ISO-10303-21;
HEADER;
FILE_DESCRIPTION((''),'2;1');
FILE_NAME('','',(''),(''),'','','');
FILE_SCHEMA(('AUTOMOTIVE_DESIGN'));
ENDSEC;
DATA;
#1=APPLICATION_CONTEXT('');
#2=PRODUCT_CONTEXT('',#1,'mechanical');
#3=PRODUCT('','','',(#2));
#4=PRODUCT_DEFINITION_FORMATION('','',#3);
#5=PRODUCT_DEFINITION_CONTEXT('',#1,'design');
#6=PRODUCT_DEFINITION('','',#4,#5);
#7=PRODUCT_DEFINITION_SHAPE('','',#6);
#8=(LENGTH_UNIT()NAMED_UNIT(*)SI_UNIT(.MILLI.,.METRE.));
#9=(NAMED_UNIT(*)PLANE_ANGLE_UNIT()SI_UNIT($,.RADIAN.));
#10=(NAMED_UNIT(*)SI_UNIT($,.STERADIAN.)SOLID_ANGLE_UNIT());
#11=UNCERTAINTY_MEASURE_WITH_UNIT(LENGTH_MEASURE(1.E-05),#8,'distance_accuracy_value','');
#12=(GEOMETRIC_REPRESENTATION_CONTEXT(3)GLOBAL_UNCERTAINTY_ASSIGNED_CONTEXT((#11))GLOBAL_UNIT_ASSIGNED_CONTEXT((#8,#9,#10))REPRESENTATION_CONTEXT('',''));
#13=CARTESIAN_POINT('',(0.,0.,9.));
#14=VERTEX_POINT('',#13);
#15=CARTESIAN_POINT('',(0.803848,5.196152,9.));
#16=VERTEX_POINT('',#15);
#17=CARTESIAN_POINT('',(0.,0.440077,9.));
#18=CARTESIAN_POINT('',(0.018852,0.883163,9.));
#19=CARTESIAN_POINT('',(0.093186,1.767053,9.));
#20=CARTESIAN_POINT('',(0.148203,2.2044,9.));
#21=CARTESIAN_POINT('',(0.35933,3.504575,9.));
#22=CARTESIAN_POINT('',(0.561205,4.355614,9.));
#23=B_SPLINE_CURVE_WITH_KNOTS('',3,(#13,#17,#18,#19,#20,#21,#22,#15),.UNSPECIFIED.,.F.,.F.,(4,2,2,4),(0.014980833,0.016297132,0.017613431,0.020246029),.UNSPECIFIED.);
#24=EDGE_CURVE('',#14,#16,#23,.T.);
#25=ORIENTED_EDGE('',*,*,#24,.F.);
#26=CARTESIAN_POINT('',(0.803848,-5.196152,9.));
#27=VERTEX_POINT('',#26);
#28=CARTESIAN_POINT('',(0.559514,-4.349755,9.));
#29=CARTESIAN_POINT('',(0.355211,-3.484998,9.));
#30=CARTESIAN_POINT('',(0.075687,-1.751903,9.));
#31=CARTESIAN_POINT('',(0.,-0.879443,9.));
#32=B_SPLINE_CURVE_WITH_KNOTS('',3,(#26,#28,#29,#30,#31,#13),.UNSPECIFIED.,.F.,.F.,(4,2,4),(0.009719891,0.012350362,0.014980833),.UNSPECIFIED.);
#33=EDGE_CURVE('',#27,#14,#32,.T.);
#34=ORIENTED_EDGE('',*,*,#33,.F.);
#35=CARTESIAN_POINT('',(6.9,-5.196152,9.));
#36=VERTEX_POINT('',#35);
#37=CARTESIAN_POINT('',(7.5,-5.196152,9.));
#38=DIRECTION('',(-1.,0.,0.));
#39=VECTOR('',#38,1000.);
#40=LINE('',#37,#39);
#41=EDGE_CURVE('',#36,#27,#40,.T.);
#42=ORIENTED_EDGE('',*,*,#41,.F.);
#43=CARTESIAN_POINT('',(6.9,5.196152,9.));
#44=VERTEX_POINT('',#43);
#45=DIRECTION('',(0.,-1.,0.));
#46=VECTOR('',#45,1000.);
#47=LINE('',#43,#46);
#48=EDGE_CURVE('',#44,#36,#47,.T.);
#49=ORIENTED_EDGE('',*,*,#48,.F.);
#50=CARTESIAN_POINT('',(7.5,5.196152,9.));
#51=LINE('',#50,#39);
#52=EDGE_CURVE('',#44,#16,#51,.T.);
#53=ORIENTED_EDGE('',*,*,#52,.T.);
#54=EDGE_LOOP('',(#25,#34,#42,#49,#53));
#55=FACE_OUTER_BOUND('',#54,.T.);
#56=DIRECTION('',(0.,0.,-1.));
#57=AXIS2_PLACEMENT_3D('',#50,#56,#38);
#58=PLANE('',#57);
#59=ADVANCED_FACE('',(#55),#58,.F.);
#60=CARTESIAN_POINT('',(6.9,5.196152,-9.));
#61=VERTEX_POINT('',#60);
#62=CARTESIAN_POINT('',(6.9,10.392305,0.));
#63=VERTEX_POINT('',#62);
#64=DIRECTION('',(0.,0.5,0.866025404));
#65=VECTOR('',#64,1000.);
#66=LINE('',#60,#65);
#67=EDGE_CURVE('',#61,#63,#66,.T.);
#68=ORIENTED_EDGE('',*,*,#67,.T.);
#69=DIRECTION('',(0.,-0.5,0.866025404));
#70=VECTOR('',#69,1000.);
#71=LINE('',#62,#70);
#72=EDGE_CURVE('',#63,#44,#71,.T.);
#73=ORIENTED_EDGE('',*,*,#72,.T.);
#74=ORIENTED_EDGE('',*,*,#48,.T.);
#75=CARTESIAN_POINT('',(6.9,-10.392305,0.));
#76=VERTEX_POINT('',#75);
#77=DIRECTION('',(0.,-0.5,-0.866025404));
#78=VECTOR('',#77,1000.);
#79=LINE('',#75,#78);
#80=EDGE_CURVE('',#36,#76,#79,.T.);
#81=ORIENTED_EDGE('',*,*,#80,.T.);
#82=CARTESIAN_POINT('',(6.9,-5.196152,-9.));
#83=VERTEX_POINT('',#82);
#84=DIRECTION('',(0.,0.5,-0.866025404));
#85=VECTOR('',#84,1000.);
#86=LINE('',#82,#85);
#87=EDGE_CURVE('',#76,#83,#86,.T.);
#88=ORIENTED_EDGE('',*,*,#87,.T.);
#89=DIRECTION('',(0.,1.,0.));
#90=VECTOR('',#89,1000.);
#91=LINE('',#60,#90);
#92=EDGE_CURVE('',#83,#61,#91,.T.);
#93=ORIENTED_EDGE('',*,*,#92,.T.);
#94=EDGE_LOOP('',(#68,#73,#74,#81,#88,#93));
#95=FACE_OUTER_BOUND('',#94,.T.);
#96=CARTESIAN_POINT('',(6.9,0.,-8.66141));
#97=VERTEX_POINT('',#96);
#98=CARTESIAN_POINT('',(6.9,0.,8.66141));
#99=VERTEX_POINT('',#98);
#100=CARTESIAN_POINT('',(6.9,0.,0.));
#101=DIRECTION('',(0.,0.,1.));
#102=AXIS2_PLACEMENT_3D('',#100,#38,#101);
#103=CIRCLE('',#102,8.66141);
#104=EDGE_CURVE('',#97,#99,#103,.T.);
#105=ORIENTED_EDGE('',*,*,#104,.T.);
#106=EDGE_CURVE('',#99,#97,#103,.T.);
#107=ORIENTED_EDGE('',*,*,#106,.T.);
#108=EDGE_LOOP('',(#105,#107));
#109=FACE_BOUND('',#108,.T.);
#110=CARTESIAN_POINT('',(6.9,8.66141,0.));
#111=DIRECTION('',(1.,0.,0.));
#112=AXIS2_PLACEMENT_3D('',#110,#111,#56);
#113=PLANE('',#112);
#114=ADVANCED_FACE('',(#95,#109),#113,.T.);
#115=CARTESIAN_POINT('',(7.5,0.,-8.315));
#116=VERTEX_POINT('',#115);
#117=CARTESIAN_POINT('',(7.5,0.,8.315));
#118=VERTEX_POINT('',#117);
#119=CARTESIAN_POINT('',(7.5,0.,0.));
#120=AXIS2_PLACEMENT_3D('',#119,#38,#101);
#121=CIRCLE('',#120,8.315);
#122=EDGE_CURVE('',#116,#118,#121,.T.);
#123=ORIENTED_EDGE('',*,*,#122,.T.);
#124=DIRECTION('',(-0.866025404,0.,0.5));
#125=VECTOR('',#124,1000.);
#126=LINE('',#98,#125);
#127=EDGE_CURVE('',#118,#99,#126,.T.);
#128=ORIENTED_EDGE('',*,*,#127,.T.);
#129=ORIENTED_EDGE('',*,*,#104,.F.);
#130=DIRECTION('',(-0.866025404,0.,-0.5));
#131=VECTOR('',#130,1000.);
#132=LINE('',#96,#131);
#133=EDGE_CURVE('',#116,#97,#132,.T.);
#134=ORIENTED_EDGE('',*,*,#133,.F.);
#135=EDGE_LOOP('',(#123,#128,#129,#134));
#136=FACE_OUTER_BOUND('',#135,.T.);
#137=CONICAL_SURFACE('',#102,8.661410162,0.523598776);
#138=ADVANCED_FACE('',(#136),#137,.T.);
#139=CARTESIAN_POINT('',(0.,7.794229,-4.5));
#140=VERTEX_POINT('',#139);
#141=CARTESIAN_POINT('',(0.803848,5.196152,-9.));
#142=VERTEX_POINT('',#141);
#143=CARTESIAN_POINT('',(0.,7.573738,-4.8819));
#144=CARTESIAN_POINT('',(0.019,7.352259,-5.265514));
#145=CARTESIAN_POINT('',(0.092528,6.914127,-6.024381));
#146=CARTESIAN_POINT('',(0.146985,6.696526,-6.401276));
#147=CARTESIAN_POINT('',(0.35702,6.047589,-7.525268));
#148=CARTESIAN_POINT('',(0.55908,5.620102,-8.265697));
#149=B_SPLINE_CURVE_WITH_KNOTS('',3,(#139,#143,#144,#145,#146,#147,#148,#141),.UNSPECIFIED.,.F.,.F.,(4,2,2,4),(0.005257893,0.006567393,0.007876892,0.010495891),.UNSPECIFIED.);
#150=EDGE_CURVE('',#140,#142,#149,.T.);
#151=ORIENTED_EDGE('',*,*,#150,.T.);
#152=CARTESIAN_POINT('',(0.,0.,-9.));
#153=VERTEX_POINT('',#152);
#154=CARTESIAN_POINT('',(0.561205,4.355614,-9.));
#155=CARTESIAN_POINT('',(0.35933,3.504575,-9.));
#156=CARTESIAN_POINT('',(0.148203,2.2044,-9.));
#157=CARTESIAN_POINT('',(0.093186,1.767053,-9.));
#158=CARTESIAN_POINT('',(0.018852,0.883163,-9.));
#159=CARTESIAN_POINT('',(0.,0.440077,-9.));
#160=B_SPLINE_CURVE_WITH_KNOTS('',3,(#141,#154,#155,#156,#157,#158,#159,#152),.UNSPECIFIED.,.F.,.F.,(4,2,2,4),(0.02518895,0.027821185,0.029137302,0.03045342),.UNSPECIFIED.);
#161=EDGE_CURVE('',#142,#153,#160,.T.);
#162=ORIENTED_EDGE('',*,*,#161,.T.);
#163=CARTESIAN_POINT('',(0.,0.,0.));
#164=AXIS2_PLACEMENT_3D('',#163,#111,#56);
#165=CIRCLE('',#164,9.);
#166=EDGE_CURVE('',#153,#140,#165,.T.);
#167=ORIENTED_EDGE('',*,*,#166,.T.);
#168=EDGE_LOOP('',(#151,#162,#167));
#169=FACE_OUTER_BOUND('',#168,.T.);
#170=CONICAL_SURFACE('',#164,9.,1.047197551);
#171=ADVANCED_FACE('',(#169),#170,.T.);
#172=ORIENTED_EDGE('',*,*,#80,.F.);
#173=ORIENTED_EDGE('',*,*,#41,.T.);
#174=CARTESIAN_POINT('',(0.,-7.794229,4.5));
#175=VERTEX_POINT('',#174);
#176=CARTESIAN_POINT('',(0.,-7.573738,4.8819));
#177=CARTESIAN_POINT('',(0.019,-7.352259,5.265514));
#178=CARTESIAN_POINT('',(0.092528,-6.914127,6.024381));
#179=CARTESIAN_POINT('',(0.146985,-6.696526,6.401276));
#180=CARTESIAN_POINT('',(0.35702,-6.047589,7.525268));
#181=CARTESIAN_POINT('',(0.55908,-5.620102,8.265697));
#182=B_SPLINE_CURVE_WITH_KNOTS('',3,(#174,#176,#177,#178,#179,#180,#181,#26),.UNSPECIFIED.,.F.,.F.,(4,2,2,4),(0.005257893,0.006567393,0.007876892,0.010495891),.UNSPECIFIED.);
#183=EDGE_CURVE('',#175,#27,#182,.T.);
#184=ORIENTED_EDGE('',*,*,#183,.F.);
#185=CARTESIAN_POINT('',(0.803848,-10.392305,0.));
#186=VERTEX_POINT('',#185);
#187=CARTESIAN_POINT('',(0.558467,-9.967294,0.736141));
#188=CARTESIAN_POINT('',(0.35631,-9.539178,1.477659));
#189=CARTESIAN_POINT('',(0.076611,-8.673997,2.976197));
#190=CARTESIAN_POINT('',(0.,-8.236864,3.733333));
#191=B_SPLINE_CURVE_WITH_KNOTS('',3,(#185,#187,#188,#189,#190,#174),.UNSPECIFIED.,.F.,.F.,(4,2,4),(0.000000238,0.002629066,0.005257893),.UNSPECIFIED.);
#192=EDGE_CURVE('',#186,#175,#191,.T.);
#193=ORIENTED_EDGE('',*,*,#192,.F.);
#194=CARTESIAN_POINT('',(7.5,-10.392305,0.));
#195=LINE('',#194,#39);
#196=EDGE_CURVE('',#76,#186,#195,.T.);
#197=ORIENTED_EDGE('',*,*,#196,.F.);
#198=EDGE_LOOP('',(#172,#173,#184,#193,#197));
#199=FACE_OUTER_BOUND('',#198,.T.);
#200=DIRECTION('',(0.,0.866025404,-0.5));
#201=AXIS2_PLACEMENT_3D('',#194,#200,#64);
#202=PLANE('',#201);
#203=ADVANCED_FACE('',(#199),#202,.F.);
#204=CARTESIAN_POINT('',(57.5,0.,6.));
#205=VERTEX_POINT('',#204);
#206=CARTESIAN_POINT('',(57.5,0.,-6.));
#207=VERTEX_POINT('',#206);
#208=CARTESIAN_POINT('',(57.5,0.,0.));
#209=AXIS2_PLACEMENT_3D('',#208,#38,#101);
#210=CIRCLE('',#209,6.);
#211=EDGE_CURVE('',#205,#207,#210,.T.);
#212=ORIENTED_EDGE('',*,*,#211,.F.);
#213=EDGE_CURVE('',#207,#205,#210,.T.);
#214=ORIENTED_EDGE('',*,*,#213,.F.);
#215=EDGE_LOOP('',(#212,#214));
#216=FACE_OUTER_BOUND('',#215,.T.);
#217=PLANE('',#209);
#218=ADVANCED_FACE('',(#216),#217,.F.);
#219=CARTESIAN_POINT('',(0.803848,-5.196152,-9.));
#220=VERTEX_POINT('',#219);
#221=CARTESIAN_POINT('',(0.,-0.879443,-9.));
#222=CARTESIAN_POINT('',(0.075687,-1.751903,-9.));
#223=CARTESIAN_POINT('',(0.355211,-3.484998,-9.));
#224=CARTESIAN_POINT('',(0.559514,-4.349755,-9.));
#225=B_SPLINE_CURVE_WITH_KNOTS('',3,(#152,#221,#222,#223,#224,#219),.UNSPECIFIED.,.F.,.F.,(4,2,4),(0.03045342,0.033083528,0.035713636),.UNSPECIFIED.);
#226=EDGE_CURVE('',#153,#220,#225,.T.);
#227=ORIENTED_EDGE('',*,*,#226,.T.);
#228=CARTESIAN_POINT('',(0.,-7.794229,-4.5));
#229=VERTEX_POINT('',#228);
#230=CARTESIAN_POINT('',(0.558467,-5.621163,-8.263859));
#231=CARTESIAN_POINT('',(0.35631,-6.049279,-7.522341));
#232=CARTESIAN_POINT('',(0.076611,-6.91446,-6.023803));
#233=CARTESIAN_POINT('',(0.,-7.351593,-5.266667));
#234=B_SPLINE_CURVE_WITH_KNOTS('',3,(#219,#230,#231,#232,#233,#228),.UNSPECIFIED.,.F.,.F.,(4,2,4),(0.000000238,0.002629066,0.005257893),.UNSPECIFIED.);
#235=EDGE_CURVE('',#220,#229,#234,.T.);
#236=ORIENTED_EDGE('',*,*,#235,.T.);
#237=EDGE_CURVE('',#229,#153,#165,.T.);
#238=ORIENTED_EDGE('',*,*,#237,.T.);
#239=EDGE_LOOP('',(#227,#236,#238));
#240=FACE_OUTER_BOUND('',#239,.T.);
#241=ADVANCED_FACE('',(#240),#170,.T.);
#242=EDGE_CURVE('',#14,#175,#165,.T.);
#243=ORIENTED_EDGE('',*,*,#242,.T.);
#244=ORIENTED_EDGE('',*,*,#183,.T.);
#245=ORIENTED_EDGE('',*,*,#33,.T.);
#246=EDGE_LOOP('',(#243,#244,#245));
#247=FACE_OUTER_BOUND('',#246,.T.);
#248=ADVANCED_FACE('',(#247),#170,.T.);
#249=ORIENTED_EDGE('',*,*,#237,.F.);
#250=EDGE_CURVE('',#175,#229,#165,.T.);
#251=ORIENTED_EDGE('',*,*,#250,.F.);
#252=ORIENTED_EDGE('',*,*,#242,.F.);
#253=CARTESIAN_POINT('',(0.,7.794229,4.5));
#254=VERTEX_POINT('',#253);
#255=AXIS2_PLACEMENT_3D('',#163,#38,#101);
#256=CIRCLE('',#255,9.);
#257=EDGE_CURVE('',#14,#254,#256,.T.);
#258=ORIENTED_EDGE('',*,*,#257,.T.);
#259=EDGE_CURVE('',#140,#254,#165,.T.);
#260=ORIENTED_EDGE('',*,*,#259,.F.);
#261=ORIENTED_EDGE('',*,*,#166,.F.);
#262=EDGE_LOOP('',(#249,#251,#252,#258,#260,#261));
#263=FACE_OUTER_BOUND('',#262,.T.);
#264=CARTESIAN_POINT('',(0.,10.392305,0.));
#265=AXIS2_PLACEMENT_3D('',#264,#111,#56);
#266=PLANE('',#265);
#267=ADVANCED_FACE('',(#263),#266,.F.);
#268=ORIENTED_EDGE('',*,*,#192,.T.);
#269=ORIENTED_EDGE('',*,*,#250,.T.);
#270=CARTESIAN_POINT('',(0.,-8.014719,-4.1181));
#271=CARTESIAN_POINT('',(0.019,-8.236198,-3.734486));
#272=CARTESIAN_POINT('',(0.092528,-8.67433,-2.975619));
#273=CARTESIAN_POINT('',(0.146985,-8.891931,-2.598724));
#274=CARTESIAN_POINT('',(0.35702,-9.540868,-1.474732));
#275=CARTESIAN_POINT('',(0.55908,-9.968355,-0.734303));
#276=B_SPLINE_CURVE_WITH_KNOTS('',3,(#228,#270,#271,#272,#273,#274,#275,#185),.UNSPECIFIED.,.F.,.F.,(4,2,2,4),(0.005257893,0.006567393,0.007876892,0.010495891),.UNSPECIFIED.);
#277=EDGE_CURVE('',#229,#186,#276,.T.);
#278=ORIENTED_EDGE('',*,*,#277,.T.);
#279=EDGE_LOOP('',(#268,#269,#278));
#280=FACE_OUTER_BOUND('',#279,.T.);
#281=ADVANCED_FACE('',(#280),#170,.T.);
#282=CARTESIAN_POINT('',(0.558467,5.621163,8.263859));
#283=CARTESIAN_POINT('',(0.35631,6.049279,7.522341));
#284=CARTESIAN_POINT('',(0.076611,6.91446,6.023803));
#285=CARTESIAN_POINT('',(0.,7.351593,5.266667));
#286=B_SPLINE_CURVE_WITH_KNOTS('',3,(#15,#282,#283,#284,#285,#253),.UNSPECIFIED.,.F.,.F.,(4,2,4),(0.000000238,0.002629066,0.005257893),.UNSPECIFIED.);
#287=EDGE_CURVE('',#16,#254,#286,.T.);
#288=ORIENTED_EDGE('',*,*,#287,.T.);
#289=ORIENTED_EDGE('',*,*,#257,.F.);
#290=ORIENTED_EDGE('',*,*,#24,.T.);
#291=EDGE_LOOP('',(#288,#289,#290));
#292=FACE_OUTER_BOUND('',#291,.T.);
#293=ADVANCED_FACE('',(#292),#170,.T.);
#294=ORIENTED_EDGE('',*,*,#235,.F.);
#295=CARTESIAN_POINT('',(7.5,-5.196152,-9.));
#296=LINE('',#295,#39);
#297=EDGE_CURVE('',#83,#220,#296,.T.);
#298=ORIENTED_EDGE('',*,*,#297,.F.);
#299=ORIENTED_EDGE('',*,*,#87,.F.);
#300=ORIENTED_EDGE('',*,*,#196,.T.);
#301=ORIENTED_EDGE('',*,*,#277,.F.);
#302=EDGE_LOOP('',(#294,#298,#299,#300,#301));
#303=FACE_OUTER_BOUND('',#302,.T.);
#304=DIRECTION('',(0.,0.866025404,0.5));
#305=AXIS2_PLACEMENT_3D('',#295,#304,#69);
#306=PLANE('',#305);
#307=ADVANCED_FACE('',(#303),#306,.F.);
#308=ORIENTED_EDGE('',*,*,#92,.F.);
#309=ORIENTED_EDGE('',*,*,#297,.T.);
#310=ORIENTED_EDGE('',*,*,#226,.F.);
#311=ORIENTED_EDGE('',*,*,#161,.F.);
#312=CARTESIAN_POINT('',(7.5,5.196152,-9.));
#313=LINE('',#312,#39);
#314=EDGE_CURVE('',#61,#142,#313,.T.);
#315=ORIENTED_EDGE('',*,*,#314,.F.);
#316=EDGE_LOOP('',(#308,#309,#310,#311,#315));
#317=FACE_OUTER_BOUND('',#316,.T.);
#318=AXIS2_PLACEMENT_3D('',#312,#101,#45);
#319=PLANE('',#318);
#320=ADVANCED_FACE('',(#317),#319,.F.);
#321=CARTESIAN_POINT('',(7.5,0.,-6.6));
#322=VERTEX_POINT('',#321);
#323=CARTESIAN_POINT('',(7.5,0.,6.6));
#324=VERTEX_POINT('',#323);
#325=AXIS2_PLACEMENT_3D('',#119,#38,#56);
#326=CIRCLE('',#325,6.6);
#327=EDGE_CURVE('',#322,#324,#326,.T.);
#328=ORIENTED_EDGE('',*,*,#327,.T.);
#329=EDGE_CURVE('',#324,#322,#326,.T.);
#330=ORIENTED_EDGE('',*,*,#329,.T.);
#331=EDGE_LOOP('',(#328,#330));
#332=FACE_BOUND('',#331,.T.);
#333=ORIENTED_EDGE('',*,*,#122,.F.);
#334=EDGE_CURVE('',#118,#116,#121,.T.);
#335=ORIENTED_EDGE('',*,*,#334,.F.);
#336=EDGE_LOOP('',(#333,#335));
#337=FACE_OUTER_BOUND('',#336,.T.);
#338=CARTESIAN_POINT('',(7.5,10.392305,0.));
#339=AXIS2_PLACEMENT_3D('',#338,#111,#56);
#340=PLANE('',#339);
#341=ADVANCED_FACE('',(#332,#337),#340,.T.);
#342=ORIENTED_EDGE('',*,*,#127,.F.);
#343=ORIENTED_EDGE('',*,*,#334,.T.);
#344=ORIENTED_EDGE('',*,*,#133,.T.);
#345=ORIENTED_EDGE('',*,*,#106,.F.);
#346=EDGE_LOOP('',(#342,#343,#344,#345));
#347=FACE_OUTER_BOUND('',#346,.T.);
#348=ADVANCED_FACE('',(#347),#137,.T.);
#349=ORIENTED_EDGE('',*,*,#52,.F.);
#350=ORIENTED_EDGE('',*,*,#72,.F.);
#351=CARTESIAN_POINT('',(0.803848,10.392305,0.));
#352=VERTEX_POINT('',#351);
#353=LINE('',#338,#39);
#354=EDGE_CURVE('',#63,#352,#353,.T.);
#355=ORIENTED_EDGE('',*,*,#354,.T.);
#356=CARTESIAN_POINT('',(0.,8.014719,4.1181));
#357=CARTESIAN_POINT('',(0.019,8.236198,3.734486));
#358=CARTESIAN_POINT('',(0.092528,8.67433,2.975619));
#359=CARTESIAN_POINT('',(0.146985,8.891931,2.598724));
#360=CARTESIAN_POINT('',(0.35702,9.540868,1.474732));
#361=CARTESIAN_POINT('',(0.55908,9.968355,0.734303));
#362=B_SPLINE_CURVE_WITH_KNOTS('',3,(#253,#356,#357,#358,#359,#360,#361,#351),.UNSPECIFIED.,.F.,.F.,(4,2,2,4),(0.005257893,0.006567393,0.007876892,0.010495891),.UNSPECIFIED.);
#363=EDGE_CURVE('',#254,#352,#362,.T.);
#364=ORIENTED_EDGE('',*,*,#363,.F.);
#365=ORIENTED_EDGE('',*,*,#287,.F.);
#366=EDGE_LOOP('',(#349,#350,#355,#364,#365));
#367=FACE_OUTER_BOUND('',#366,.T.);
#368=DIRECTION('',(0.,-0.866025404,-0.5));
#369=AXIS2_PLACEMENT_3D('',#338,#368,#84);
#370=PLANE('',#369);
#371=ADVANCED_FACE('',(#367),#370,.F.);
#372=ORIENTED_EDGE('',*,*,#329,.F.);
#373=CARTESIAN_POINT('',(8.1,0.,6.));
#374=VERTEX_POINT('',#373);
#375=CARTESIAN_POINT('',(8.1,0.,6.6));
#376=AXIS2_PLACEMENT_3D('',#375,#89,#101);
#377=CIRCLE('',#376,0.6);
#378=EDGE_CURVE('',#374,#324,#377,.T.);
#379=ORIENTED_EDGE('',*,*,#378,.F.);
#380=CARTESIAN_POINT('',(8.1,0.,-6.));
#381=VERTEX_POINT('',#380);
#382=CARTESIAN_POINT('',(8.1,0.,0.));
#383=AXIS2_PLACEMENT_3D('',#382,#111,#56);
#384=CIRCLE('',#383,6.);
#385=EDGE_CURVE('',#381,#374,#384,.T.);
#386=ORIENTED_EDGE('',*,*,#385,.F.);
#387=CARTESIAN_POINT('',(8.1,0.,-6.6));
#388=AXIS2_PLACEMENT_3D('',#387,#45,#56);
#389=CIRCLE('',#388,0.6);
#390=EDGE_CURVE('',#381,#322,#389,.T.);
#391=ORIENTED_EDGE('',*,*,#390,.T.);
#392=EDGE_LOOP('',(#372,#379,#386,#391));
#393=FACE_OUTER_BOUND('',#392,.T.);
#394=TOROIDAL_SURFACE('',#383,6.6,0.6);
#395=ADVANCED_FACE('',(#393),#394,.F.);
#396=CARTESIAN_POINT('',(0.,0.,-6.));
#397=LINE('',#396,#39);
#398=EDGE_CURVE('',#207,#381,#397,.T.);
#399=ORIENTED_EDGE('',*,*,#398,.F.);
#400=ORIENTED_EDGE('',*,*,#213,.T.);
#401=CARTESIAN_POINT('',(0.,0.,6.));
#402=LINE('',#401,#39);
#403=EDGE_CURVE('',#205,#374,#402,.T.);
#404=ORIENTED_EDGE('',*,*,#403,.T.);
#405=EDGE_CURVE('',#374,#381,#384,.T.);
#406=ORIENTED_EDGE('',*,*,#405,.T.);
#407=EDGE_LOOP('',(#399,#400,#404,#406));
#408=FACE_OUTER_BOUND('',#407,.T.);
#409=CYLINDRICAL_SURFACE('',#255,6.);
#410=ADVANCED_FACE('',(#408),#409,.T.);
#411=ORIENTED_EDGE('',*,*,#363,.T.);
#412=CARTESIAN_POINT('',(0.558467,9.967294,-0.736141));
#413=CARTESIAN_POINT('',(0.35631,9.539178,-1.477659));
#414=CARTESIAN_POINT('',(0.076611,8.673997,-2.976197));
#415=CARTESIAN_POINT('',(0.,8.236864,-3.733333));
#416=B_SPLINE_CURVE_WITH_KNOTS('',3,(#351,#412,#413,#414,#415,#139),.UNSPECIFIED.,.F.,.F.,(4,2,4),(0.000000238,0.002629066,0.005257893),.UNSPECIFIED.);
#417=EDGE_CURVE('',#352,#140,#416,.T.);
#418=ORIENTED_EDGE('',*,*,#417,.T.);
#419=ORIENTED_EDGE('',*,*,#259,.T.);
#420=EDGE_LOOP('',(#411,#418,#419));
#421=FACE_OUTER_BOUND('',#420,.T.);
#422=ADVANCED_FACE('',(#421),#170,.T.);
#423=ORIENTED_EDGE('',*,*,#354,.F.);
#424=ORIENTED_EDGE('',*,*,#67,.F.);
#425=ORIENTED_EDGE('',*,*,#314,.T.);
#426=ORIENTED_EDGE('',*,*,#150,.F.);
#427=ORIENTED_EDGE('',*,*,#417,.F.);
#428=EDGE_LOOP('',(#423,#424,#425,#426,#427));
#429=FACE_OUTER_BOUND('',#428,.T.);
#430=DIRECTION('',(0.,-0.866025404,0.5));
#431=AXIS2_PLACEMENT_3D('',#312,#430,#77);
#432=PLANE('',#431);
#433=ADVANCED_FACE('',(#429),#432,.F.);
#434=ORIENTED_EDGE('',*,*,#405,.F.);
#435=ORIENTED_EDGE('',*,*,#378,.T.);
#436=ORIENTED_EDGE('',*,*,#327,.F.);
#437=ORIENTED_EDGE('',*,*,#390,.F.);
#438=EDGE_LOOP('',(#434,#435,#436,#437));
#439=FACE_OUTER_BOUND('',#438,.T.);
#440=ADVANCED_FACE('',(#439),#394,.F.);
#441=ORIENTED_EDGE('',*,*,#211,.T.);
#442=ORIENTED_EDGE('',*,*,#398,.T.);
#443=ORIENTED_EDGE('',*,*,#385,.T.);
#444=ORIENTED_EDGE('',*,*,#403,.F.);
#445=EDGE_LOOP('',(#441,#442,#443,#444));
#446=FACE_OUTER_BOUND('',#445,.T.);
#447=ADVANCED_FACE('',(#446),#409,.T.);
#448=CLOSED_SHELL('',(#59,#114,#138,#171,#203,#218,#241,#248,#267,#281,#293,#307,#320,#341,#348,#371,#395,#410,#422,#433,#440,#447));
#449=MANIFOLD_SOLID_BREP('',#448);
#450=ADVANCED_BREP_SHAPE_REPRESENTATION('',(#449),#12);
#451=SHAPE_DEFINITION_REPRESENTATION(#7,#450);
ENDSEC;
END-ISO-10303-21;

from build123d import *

# Parameters (mm, degrees)
EXTRUDE_387_DEPTH = 7.5
FILLET_1280_R     = 0.6


with BuildPart() as part:
    # 草图1 → Extrude 387 (new body)
    with BuildSketch(Plane(origin=(0, 0, 0), x_dir=(0, 0, -1), z_dir=(1, 0, 0))):
        Polygon((9, 5.196152423), (9, -5.196152423), (0, -10.392304845), (-9, -5.196152423), (-9, 5.196152423), (0, 10.392304845), align=None)
    extrude(amount=EXTRUDE_387_DEPTH)

    # 草图2 → 凸台-旋转1 (revolve)
    with BuildSketch(Plane.XY, mode=Mode.PRIVATE) as revolve_1_sk:
        Polygon((0, 0), (57.5, 0), (57.5, 4.4845), (57.5, 6), (27.5, 6), (0, 6), align=None)
    revolve(revolve_1_sk.sketch.rotate(Axis((0, 0, 0), (1, 0, 0)), 90), axis=Axis((0, 0, 0), (1, 0, 0)))

    # 草图3 → 切除-旋转1 (revolve, cut)
    with BuildSketch(Plane.XY):
        Polygon((0, 9), (3.690598923, 15.392304845), (3.690598923, 20.392304845), (-10, 20.392304845), (-10, 9), align=None)
    revolve(axis=Axis((0, 0, 0), (1, 0, 0)), mode=Mode.SUBTRACT)

    # 草图4 → 切除-旋转3 (revolve, cut)
    with BuildSketch(Plane.XY, mode=Mode.PRIVATE) as cut_revolve_3_sk:
        Polygon((7.5, 8.315), (6.9, 8.661410162), (6.9, 10.392304845), (7.5, 10.392304845), align=None)
    revolve(cut_revolve_3_sk.sketch.rotate(Axis((0, 0, 0), (1, 0, 0)), 90), axis=Axis((0, 0, 0), (1, 0, 0)), mode=Mode.SUBTRACT)

    # Fillet 1280
    fillet_1280_edges = [part.edges().sort_by_distance(p)[0] for p in [
        (7.5, 0, -6),
    ]]
    fillet(fillet_1280_edges, radius=FILLET_1280_R)


solid = part.part
